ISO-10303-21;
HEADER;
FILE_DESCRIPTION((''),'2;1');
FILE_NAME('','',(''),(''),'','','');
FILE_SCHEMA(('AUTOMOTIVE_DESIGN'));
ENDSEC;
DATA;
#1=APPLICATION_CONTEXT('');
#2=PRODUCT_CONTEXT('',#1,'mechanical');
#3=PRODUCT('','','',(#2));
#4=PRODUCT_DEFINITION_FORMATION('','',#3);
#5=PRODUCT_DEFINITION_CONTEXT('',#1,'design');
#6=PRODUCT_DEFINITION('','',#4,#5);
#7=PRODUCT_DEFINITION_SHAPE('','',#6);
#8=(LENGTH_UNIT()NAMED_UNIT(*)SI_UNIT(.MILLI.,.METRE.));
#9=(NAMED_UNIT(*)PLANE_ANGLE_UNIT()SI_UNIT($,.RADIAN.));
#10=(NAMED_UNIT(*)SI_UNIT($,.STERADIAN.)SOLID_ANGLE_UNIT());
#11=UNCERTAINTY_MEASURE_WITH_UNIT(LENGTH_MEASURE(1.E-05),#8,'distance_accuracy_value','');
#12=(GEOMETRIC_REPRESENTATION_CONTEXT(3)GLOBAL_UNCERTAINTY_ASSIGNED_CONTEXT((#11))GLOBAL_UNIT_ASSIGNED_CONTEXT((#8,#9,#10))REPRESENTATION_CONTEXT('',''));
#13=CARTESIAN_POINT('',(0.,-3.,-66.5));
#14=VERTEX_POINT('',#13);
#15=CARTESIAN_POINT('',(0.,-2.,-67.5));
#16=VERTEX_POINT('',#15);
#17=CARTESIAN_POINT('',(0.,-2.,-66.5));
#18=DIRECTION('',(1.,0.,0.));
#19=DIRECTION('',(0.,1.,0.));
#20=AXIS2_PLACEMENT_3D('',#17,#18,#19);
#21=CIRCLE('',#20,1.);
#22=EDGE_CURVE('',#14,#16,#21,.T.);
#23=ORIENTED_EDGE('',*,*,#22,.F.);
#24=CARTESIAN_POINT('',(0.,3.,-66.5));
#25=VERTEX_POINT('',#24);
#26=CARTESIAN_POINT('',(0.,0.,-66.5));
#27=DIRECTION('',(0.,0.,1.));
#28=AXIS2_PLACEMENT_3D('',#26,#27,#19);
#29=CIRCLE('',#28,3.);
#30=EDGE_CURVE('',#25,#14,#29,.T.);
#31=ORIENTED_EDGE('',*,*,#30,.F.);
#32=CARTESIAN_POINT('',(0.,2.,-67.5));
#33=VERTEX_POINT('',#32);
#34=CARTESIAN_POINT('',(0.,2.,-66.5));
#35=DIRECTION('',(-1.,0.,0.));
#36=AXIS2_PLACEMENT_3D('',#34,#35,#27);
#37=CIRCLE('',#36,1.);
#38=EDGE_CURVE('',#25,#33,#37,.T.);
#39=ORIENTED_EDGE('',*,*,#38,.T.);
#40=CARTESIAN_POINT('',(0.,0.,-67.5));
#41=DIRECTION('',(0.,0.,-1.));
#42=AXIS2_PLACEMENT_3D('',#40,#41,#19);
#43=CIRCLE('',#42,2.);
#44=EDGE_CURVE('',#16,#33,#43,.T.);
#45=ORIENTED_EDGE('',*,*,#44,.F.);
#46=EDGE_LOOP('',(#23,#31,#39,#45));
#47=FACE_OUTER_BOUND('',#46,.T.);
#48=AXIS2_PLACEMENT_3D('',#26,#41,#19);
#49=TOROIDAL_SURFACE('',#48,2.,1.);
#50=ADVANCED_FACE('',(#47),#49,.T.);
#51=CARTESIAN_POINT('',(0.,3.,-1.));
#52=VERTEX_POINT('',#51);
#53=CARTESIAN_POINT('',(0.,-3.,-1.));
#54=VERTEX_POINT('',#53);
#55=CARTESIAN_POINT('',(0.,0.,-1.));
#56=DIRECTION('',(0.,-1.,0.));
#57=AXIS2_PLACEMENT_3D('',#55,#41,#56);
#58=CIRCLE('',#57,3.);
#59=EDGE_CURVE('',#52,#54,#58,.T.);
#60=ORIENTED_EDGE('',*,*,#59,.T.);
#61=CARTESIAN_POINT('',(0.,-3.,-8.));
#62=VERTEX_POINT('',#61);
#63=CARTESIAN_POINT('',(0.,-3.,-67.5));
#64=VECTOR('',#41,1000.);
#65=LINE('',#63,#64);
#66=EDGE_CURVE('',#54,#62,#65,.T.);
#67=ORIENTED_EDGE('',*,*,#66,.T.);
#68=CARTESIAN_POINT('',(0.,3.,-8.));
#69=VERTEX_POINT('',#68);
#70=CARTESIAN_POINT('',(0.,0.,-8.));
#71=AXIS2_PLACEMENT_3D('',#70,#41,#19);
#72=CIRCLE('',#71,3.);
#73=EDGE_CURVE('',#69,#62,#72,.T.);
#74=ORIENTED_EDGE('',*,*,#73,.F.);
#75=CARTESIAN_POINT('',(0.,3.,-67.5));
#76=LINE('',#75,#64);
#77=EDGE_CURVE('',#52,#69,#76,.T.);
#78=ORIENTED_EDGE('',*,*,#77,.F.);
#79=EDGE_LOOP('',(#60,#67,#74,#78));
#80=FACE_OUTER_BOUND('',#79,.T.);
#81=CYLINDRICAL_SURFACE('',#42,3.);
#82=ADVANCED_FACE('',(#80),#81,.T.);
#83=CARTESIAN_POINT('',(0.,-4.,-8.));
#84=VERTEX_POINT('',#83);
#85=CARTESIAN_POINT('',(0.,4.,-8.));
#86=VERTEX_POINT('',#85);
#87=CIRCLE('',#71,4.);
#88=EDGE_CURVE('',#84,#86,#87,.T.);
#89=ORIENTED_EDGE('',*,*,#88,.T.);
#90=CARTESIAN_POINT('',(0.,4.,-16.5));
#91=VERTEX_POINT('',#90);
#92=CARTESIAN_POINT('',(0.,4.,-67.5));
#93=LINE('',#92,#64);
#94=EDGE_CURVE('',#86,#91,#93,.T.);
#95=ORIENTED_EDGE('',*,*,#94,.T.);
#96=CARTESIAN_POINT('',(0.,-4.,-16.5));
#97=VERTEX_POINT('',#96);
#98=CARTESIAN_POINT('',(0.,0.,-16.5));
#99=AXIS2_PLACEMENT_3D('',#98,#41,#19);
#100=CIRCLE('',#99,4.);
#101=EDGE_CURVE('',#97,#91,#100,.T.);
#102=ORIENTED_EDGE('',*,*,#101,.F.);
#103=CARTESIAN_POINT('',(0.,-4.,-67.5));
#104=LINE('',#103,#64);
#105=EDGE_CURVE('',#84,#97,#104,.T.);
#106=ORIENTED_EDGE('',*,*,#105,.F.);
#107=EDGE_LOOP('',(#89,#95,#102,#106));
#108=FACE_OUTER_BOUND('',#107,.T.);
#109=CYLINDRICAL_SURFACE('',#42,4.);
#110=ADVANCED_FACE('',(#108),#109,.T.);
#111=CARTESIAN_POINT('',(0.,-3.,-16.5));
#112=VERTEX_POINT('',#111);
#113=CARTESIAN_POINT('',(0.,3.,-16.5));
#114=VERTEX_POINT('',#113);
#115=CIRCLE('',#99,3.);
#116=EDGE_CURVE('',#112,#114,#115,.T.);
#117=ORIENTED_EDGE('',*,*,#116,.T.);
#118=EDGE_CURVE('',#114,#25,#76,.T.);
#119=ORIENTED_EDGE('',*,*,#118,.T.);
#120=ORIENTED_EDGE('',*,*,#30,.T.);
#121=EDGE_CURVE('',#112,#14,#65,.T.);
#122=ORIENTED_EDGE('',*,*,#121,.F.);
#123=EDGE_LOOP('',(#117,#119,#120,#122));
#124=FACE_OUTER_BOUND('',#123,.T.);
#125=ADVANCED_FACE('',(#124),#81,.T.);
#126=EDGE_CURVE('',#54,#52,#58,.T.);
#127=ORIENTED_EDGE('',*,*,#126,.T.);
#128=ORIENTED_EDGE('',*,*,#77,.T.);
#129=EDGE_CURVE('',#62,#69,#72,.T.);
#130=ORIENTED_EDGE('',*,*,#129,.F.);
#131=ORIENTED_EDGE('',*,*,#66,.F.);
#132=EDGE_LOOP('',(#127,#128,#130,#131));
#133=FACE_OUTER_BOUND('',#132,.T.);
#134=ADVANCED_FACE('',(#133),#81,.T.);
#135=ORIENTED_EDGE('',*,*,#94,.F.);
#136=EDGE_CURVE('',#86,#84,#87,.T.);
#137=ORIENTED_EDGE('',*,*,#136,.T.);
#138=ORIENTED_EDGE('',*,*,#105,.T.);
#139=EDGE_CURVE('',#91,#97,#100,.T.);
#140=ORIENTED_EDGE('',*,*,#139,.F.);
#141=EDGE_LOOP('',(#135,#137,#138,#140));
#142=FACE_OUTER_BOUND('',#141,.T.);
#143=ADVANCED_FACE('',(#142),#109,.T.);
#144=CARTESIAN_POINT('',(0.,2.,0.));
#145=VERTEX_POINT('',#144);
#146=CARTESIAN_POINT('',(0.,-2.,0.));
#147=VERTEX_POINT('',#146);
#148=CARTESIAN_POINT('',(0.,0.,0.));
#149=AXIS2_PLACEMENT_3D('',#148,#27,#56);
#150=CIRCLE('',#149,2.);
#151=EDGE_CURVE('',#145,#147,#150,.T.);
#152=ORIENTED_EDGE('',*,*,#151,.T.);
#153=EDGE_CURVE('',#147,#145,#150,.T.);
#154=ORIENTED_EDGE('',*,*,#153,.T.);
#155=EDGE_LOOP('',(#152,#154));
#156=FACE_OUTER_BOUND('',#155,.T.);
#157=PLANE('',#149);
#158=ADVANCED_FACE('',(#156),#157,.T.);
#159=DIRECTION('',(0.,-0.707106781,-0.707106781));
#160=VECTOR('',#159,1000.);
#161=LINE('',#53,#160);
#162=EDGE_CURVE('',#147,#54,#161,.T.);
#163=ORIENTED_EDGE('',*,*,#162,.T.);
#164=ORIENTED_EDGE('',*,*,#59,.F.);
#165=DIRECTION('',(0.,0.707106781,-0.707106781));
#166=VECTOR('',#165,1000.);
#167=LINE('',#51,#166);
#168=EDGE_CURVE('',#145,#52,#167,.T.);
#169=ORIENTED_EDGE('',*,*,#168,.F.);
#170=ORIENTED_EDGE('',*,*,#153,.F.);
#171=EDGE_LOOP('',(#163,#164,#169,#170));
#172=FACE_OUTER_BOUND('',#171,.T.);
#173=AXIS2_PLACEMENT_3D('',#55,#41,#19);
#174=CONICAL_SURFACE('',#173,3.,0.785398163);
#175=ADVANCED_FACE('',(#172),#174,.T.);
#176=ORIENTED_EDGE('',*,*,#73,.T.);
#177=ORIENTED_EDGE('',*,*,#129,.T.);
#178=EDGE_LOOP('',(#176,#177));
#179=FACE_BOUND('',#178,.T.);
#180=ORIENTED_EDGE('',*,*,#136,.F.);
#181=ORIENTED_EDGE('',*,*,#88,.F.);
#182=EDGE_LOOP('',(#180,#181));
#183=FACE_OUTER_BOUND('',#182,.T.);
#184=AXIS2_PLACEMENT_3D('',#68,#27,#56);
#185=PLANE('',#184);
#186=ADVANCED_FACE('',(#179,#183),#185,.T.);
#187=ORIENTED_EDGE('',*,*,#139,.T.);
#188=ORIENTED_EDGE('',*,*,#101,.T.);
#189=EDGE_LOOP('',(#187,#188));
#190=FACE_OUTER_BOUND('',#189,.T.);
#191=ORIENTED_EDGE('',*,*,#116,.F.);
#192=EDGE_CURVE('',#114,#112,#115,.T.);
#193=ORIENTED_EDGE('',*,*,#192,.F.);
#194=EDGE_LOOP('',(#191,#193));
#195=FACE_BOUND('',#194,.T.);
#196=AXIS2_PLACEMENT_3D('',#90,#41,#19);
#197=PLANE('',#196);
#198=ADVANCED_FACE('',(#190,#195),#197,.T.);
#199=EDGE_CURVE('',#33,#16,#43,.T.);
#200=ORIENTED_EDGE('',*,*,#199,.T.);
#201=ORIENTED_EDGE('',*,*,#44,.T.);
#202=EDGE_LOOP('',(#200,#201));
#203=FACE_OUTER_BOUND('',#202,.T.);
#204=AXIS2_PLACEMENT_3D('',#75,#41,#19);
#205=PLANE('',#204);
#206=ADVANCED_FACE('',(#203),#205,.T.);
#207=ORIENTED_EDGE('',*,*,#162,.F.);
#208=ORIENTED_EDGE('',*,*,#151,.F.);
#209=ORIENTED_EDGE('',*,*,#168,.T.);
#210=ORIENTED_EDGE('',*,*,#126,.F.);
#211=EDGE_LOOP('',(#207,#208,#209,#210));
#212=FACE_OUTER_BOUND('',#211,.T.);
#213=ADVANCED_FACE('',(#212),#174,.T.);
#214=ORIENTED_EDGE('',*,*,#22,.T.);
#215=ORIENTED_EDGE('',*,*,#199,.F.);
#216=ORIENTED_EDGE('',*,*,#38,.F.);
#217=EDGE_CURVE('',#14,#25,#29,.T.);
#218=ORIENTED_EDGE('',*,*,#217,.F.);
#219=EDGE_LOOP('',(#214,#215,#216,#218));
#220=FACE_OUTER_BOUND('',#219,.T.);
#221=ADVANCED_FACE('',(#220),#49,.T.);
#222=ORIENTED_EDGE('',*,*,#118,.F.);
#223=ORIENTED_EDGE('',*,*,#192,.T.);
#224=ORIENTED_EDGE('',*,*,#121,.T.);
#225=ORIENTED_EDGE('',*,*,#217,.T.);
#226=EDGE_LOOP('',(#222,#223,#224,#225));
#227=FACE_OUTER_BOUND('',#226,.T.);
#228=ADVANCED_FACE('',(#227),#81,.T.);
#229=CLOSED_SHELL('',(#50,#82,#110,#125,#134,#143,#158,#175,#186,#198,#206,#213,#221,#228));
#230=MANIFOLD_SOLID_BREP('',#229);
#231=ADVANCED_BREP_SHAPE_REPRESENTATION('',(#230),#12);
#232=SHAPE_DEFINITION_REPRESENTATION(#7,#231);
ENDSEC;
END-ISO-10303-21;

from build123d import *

# Parameters (mm, degrees)
FILLET_1_R     = 1
CHAMFER_1_SIZE = 1


with BuildPart() as part:
    # 草图1 → 旋转1 (revolve)
    with BuildSketch(Plane(origin=(0, 0, 0), x_dir=(0, 0, -1), z_dir=(1, 0, 0))):
        Polygon((0, 0), (0, 3), (8, 3), (8, 4), (16.5, 4), (16.5, 3), (67.5, 3), (67.5, 0), align=None)
    revolve(axis=Axis((0, 0, -67.5), (0, 0, 1)))

    # 圆角1
    fillet_1_edges = [part.edges().sort_by_distance(p)[0] for p in [
        (0, -3, -67.5),
    ]]
    fillet(fillet_1_edges, radius=FILLET_1_R)

    # 倒角1
    chamfer_1_edges = [part.edges().sort_by_distance(p)[0] for p in [
        (0, -3, 0),
    ]]
    chamfer(chamfer_1_edges, length=CHAMFER_1_SIZE)


solid = part.part
